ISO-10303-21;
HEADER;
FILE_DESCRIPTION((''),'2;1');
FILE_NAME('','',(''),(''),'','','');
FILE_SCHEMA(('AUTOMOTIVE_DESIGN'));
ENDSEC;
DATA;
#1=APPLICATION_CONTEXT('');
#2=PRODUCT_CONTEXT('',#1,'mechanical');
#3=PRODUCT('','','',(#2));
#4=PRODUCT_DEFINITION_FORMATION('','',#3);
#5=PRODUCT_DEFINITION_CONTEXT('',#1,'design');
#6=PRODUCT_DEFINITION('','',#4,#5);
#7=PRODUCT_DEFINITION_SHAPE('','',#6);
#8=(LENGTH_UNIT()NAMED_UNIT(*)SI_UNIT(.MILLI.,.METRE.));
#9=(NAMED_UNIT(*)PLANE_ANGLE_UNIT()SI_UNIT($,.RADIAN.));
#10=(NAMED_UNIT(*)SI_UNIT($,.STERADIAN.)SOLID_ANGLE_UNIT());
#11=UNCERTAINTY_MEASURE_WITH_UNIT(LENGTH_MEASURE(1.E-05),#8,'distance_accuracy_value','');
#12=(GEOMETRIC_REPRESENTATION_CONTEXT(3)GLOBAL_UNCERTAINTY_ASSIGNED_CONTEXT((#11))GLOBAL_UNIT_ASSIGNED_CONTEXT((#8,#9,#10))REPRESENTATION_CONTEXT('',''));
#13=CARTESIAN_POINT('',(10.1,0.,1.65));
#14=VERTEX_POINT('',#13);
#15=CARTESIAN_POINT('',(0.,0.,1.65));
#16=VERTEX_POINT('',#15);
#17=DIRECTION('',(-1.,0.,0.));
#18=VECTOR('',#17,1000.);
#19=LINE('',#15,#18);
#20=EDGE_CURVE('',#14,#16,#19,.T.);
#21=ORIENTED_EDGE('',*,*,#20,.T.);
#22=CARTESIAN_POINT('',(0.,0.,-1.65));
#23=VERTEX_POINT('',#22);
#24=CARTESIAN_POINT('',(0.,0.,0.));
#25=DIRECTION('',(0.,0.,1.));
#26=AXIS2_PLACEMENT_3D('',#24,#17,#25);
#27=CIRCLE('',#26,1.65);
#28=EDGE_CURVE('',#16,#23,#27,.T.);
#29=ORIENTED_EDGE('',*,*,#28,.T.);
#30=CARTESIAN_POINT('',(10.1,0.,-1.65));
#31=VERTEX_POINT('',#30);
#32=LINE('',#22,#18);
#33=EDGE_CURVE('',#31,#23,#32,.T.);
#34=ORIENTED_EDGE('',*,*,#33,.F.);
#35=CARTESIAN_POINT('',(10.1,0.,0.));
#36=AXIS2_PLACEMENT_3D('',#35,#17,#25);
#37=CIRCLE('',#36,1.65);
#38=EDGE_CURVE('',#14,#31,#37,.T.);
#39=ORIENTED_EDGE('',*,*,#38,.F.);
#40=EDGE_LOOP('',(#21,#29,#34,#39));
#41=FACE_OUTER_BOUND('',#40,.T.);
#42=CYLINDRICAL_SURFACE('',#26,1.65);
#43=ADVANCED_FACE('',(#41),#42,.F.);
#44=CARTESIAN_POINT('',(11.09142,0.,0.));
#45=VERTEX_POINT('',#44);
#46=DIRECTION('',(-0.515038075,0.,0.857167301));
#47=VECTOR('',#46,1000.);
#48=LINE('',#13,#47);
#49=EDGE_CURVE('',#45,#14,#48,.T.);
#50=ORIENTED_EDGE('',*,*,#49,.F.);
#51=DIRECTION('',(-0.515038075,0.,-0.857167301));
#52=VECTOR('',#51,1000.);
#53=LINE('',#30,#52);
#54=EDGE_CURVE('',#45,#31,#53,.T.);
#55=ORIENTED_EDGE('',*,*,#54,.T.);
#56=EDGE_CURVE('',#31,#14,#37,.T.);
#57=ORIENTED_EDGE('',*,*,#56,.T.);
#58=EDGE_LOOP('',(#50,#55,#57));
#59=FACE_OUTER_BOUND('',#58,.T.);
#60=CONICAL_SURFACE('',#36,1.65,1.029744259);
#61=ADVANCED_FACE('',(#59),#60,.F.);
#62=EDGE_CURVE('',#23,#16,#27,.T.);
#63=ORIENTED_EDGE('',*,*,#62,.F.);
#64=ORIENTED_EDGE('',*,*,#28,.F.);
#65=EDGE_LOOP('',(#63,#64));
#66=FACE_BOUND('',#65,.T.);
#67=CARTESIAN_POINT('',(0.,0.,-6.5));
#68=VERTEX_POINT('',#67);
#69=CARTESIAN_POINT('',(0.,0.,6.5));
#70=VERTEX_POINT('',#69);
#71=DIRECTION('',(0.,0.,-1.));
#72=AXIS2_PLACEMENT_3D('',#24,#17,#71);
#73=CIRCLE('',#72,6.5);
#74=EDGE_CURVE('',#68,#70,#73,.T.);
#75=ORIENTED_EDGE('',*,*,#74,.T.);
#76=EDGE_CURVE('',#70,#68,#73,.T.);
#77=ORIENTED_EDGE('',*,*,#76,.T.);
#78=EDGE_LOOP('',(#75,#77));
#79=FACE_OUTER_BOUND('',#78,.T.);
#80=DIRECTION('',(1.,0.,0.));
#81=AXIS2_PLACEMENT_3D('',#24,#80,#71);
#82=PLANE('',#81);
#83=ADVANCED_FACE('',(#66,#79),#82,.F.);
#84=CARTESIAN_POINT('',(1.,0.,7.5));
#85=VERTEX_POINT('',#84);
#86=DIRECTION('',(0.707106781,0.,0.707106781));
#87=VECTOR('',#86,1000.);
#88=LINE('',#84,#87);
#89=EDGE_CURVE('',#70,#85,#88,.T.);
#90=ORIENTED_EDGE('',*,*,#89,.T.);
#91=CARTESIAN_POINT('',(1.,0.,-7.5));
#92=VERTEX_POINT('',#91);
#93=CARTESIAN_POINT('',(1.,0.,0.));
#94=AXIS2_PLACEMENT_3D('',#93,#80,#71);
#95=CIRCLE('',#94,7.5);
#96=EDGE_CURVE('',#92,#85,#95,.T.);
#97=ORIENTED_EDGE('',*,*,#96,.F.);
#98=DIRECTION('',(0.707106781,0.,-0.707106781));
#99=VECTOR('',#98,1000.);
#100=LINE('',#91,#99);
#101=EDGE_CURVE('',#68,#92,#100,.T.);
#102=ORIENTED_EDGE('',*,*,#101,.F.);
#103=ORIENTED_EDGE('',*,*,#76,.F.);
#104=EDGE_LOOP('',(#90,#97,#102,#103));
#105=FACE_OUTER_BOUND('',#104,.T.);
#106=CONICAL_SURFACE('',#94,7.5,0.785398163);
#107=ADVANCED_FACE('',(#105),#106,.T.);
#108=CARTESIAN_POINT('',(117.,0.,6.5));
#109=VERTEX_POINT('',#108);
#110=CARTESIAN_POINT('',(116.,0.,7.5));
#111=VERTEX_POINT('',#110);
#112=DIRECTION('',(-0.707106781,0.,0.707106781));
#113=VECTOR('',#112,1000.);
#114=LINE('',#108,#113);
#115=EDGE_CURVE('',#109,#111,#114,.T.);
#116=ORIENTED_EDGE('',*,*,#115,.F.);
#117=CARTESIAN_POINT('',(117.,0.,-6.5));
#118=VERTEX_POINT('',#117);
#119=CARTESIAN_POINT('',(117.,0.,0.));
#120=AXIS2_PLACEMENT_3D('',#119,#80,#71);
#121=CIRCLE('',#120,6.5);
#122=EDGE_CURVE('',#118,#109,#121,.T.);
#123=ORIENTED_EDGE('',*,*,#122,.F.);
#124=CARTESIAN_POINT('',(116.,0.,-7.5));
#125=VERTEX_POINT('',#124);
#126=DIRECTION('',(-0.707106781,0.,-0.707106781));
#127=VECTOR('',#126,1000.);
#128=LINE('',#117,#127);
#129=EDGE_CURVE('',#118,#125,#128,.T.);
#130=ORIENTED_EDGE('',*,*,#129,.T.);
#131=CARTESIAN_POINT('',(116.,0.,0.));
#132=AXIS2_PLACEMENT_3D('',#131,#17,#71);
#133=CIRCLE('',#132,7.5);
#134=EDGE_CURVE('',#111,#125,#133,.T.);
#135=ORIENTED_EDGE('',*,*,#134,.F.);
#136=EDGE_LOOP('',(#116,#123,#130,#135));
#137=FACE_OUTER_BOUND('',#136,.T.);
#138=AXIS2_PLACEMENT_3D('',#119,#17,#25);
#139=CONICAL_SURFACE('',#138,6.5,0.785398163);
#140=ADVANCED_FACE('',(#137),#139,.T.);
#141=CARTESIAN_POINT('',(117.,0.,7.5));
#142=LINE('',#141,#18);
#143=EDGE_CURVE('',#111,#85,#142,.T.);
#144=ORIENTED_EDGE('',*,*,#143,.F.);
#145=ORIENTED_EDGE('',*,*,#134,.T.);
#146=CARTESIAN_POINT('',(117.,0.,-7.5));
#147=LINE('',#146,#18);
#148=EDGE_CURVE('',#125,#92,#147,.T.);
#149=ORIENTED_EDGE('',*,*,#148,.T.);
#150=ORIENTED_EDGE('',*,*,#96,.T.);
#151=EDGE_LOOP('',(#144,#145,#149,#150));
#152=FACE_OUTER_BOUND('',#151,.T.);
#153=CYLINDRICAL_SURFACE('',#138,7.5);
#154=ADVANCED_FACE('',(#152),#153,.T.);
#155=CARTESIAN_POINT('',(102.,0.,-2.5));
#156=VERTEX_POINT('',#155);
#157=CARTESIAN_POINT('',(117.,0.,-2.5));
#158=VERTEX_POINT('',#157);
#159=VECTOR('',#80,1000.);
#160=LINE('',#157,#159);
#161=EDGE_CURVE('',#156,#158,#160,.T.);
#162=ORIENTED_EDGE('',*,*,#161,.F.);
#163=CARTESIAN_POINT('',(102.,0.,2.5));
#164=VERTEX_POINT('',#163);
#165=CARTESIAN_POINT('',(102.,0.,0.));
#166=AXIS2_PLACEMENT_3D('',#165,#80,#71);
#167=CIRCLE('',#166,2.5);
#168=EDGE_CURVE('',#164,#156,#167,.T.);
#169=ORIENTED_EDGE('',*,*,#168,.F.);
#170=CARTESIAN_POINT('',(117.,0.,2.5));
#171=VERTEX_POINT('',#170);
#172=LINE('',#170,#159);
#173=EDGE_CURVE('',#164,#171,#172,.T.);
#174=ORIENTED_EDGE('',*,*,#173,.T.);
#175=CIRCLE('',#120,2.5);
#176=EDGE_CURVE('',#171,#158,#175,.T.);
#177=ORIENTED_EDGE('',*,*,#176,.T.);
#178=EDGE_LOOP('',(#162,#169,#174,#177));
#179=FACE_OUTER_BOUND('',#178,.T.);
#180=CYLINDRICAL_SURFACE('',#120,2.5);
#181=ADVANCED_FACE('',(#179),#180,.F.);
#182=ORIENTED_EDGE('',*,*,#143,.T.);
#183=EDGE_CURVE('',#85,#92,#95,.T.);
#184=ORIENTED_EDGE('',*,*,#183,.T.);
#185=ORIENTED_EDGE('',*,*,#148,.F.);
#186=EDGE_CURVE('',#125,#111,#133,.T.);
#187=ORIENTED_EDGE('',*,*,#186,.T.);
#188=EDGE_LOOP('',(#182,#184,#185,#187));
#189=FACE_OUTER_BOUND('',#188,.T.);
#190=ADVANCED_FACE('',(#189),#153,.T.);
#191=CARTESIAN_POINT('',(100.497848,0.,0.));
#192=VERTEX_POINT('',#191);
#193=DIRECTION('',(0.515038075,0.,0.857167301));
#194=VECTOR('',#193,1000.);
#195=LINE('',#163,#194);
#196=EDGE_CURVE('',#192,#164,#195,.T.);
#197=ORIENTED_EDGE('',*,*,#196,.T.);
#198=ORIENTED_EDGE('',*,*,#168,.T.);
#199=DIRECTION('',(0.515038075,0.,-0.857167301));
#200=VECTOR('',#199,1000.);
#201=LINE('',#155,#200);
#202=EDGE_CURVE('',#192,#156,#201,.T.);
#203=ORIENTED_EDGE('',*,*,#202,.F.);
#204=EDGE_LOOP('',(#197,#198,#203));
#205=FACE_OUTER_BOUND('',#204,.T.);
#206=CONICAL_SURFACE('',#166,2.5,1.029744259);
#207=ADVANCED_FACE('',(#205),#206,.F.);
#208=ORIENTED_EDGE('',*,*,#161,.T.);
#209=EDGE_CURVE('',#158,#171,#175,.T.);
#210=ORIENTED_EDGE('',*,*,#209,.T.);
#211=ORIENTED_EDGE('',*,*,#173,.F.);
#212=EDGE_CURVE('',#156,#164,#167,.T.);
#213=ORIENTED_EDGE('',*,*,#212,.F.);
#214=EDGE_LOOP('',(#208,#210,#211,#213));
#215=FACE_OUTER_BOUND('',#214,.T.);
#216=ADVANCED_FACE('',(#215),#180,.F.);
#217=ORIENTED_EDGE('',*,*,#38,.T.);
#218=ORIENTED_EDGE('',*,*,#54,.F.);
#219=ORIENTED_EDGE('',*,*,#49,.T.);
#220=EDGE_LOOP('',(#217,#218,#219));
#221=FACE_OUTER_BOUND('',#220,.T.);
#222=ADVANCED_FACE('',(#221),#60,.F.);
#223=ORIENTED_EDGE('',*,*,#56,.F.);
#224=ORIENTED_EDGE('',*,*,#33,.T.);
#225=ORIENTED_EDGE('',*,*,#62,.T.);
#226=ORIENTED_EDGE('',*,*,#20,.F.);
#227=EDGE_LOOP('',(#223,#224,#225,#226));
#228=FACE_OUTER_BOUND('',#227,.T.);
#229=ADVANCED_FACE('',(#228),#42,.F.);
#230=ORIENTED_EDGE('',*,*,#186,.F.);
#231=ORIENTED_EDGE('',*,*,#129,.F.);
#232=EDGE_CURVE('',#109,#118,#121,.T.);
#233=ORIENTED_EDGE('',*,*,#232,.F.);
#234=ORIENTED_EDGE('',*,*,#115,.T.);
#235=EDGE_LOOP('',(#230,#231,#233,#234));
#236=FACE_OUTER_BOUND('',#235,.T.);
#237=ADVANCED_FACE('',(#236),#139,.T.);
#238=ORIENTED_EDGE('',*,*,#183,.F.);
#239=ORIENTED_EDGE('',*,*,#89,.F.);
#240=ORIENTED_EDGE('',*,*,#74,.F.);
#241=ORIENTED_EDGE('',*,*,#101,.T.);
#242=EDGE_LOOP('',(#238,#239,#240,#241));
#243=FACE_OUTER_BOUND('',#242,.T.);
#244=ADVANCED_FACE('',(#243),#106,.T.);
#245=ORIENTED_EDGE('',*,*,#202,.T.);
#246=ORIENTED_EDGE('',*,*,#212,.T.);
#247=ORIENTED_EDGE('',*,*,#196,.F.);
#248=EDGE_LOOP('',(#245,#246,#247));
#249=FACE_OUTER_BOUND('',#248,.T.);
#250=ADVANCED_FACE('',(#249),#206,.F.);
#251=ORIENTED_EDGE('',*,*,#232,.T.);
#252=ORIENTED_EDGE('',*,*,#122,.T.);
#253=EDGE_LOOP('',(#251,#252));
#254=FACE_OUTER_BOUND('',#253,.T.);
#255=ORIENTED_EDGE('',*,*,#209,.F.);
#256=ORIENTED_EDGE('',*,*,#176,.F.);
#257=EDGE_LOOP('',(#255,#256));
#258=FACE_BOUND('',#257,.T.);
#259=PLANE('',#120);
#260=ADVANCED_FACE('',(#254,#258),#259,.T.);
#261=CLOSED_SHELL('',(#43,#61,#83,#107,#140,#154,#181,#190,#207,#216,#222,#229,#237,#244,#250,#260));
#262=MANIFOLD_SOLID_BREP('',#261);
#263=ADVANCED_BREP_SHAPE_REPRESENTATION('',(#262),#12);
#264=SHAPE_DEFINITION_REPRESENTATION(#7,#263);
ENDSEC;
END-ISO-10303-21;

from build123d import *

# Parameters (mm, degrees)
SKETCH_1_R             = 7.5
EXTRUDE_1_DEPTH        = 117
HOLE_WIZARD_M4_1_D     = 3.3
HOLE_WIZARD_M4_1_DEPTH = 10.1
HOLE_WIZARD_M4_1_TIP   = 0.991420021
HOLE_WIZARD_M6_1_D     = 5
HOLE_WIZARD_M6_1_DEPTH = 15
HOLE_WIZARD_M6_1_TIP   = 1.502151548
CHAMFER_1_SIZE         = 1


with BuildPart() as part:
    # 草图1 → 凸台-拉伸1 (new body)
    with BuildSketch(Plane(origin=(0, 0, 0), x_dir=(0, 0, -1), z_dir=(1, 0, 0))):
        Circle(SKETCH_1_R)
    extrude(amount=EXTRUDE_1_DEPTH)

    # M4 螺纹孔1
    with Locations(Plane.ZY):
        with Locations((0, 0)):
            Hole(HOLE_WIZARD_M4_1_D / 2, depth=HOLE_WIZARD_M4_1_DEPTH)
            with Locations((0, 0, -(HOLE_WIZARD_M4_1_DEPTH + HOLE_WIZARD_M4_1_TIP / 2))):  # 118° drill point
                Cone(0, HOLE_WIZARD_M4_1_D / 2, HOLE_WIZARD_M4_1_TIP, mode=Mode.SUBTRACT)

    # M6 螺纹孔1
    with Locations(Plane(origin=(117, 0, 0), x_dir=(0, 0, -1), z_dir=(1, 0, 0))):
        with Locations((0, 0)):
            Hole(HOLE_WIZARD_M6_1_D / 2, depth=HOLE_WIZARD_M6_1_DEPTH)
            with Locations((0, 0, -(HOLE_WIZARD_M6_1_DEPTH + HOLE_WIZARD_M6_1_TIP / 2))):  # 118° drill point
                Cone(0, HOLE_WIZARD_M6_1_D / 2, HOLE_WIZARD_M6_1_TIP, mode=Mode.SUBTRACT)

    # 倒角1
    chamfer_1_edges = [part.edges().sort_by_distance(p)[0] for p in [
        (0, 0, 7.5),
        (117, 0, 7.5),
    ]]
    chamfer(chamfer_1_edges, length=CHAMFER_1_SIZE)


solid = part.part
